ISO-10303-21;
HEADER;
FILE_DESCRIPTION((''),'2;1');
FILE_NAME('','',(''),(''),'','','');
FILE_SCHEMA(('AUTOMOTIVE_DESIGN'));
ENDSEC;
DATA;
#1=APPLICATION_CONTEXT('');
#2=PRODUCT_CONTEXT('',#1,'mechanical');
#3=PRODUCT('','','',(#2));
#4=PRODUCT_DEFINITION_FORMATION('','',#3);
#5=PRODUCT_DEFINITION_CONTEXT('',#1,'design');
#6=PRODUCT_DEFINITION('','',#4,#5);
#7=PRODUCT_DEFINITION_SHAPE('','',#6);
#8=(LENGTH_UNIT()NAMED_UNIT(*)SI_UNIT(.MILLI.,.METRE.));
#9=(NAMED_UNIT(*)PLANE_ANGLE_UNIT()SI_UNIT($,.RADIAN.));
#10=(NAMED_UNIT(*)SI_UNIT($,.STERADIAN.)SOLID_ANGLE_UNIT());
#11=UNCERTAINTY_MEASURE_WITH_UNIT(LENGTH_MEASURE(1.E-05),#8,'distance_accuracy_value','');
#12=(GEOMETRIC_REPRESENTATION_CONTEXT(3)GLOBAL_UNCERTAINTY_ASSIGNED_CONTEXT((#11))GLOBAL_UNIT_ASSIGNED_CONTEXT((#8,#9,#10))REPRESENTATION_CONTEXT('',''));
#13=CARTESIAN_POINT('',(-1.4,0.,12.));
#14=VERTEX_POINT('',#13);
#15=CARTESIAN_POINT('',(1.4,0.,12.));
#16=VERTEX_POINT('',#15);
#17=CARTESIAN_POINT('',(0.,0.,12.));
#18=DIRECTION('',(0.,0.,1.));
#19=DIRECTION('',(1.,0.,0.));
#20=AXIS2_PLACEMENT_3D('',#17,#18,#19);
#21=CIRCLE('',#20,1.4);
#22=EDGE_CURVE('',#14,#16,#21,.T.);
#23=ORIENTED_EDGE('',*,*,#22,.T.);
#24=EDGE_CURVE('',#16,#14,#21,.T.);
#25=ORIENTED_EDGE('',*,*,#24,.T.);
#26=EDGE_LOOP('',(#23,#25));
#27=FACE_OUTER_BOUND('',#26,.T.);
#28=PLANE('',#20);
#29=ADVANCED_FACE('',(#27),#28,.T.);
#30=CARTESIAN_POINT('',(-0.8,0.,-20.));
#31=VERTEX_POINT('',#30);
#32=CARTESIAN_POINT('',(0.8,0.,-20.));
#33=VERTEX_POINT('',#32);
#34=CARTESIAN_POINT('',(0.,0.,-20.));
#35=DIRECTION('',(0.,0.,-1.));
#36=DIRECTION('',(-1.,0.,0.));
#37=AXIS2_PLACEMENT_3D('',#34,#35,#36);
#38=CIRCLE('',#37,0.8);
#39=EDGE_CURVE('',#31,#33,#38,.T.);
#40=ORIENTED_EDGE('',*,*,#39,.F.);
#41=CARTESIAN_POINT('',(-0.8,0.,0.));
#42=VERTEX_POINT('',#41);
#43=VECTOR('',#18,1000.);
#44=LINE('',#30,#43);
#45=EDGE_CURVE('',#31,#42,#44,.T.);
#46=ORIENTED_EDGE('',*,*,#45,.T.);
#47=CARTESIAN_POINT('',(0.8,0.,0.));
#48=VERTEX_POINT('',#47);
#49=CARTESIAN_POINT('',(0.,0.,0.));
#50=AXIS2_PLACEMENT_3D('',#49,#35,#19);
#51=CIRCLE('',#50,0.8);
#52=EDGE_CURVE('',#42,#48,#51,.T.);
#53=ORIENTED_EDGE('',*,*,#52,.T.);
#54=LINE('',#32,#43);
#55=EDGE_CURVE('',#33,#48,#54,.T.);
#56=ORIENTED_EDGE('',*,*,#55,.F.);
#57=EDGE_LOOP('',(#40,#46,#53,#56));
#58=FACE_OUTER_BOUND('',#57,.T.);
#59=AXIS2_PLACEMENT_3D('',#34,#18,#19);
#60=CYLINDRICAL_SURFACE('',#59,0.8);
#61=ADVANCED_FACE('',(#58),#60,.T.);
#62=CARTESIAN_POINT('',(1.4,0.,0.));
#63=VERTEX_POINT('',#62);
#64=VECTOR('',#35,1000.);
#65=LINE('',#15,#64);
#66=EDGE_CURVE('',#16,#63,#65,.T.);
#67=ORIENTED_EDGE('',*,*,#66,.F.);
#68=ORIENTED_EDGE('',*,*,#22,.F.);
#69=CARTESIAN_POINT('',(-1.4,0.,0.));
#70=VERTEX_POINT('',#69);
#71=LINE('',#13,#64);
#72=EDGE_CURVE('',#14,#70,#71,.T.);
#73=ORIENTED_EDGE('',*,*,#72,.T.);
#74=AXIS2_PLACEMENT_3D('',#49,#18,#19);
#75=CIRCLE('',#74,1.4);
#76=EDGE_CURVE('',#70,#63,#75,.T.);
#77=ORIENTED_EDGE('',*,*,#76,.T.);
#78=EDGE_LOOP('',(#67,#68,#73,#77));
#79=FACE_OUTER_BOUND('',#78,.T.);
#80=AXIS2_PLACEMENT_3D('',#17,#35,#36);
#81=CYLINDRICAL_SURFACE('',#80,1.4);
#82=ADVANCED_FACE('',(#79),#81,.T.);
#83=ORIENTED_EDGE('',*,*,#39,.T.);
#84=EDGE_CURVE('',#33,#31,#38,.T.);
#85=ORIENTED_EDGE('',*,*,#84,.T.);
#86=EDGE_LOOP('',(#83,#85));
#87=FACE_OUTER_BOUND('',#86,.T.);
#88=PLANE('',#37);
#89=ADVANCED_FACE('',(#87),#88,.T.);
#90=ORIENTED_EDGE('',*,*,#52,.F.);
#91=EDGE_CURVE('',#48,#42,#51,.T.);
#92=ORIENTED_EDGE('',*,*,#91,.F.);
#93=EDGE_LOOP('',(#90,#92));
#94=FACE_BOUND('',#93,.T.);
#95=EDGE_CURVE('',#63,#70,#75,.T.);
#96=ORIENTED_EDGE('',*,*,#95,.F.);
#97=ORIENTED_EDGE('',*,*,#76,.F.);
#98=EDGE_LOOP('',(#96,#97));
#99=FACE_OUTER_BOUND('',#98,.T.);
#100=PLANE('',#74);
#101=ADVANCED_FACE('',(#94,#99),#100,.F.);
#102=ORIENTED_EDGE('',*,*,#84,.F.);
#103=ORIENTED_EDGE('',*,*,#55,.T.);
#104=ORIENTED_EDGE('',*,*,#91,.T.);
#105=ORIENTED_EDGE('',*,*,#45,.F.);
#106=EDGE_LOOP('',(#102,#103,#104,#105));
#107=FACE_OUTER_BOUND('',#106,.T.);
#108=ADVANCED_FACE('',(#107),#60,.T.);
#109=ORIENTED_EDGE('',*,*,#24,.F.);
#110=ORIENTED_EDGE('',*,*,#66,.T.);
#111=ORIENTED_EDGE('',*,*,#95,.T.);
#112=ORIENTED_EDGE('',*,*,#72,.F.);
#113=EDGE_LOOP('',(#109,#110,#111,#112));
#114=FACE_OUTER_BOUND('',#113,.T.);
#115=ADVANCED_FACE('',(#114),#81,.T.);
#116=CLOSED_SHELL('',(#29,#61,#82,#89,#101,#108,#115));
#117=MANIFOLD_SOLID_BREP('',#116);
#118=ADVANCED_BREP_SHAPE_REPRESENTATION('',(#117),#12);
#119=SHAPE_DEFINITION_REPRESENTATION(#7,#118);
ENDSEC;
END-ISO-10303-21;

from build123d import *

# Parameters (mm, degrees)
SKETCH1_R           = 1.4
BOSS_EXTRUDE1_DEPTH = 12
SKETCH2_R           = 0.8
BOSS_EXTRUDE2_DEPTH = 20


with BuildPart() as part:
    # Sketch1 → Boss-Extrude1 (new body)
    with BuildSketch(Plane.XY):
        Circle(SKETCH1_R)
    extrude(amount=BOSS_EXTRUDE1_DEPTH)

    # Sketch2 → Boss-Extrude2 (add)
    with BuildSketch(Plane(origin=(0, 0, 0), x_dir=(-1, 0, 0), z_dir=(0, 0, -1))):
        with Locations(Location((0, 0, 0), (0, 0, 180))):
            Circle(SKETCH2_R)
    extrude(amount=BOSS_EXTRUDE2_DEPTH)


solid = part.part
